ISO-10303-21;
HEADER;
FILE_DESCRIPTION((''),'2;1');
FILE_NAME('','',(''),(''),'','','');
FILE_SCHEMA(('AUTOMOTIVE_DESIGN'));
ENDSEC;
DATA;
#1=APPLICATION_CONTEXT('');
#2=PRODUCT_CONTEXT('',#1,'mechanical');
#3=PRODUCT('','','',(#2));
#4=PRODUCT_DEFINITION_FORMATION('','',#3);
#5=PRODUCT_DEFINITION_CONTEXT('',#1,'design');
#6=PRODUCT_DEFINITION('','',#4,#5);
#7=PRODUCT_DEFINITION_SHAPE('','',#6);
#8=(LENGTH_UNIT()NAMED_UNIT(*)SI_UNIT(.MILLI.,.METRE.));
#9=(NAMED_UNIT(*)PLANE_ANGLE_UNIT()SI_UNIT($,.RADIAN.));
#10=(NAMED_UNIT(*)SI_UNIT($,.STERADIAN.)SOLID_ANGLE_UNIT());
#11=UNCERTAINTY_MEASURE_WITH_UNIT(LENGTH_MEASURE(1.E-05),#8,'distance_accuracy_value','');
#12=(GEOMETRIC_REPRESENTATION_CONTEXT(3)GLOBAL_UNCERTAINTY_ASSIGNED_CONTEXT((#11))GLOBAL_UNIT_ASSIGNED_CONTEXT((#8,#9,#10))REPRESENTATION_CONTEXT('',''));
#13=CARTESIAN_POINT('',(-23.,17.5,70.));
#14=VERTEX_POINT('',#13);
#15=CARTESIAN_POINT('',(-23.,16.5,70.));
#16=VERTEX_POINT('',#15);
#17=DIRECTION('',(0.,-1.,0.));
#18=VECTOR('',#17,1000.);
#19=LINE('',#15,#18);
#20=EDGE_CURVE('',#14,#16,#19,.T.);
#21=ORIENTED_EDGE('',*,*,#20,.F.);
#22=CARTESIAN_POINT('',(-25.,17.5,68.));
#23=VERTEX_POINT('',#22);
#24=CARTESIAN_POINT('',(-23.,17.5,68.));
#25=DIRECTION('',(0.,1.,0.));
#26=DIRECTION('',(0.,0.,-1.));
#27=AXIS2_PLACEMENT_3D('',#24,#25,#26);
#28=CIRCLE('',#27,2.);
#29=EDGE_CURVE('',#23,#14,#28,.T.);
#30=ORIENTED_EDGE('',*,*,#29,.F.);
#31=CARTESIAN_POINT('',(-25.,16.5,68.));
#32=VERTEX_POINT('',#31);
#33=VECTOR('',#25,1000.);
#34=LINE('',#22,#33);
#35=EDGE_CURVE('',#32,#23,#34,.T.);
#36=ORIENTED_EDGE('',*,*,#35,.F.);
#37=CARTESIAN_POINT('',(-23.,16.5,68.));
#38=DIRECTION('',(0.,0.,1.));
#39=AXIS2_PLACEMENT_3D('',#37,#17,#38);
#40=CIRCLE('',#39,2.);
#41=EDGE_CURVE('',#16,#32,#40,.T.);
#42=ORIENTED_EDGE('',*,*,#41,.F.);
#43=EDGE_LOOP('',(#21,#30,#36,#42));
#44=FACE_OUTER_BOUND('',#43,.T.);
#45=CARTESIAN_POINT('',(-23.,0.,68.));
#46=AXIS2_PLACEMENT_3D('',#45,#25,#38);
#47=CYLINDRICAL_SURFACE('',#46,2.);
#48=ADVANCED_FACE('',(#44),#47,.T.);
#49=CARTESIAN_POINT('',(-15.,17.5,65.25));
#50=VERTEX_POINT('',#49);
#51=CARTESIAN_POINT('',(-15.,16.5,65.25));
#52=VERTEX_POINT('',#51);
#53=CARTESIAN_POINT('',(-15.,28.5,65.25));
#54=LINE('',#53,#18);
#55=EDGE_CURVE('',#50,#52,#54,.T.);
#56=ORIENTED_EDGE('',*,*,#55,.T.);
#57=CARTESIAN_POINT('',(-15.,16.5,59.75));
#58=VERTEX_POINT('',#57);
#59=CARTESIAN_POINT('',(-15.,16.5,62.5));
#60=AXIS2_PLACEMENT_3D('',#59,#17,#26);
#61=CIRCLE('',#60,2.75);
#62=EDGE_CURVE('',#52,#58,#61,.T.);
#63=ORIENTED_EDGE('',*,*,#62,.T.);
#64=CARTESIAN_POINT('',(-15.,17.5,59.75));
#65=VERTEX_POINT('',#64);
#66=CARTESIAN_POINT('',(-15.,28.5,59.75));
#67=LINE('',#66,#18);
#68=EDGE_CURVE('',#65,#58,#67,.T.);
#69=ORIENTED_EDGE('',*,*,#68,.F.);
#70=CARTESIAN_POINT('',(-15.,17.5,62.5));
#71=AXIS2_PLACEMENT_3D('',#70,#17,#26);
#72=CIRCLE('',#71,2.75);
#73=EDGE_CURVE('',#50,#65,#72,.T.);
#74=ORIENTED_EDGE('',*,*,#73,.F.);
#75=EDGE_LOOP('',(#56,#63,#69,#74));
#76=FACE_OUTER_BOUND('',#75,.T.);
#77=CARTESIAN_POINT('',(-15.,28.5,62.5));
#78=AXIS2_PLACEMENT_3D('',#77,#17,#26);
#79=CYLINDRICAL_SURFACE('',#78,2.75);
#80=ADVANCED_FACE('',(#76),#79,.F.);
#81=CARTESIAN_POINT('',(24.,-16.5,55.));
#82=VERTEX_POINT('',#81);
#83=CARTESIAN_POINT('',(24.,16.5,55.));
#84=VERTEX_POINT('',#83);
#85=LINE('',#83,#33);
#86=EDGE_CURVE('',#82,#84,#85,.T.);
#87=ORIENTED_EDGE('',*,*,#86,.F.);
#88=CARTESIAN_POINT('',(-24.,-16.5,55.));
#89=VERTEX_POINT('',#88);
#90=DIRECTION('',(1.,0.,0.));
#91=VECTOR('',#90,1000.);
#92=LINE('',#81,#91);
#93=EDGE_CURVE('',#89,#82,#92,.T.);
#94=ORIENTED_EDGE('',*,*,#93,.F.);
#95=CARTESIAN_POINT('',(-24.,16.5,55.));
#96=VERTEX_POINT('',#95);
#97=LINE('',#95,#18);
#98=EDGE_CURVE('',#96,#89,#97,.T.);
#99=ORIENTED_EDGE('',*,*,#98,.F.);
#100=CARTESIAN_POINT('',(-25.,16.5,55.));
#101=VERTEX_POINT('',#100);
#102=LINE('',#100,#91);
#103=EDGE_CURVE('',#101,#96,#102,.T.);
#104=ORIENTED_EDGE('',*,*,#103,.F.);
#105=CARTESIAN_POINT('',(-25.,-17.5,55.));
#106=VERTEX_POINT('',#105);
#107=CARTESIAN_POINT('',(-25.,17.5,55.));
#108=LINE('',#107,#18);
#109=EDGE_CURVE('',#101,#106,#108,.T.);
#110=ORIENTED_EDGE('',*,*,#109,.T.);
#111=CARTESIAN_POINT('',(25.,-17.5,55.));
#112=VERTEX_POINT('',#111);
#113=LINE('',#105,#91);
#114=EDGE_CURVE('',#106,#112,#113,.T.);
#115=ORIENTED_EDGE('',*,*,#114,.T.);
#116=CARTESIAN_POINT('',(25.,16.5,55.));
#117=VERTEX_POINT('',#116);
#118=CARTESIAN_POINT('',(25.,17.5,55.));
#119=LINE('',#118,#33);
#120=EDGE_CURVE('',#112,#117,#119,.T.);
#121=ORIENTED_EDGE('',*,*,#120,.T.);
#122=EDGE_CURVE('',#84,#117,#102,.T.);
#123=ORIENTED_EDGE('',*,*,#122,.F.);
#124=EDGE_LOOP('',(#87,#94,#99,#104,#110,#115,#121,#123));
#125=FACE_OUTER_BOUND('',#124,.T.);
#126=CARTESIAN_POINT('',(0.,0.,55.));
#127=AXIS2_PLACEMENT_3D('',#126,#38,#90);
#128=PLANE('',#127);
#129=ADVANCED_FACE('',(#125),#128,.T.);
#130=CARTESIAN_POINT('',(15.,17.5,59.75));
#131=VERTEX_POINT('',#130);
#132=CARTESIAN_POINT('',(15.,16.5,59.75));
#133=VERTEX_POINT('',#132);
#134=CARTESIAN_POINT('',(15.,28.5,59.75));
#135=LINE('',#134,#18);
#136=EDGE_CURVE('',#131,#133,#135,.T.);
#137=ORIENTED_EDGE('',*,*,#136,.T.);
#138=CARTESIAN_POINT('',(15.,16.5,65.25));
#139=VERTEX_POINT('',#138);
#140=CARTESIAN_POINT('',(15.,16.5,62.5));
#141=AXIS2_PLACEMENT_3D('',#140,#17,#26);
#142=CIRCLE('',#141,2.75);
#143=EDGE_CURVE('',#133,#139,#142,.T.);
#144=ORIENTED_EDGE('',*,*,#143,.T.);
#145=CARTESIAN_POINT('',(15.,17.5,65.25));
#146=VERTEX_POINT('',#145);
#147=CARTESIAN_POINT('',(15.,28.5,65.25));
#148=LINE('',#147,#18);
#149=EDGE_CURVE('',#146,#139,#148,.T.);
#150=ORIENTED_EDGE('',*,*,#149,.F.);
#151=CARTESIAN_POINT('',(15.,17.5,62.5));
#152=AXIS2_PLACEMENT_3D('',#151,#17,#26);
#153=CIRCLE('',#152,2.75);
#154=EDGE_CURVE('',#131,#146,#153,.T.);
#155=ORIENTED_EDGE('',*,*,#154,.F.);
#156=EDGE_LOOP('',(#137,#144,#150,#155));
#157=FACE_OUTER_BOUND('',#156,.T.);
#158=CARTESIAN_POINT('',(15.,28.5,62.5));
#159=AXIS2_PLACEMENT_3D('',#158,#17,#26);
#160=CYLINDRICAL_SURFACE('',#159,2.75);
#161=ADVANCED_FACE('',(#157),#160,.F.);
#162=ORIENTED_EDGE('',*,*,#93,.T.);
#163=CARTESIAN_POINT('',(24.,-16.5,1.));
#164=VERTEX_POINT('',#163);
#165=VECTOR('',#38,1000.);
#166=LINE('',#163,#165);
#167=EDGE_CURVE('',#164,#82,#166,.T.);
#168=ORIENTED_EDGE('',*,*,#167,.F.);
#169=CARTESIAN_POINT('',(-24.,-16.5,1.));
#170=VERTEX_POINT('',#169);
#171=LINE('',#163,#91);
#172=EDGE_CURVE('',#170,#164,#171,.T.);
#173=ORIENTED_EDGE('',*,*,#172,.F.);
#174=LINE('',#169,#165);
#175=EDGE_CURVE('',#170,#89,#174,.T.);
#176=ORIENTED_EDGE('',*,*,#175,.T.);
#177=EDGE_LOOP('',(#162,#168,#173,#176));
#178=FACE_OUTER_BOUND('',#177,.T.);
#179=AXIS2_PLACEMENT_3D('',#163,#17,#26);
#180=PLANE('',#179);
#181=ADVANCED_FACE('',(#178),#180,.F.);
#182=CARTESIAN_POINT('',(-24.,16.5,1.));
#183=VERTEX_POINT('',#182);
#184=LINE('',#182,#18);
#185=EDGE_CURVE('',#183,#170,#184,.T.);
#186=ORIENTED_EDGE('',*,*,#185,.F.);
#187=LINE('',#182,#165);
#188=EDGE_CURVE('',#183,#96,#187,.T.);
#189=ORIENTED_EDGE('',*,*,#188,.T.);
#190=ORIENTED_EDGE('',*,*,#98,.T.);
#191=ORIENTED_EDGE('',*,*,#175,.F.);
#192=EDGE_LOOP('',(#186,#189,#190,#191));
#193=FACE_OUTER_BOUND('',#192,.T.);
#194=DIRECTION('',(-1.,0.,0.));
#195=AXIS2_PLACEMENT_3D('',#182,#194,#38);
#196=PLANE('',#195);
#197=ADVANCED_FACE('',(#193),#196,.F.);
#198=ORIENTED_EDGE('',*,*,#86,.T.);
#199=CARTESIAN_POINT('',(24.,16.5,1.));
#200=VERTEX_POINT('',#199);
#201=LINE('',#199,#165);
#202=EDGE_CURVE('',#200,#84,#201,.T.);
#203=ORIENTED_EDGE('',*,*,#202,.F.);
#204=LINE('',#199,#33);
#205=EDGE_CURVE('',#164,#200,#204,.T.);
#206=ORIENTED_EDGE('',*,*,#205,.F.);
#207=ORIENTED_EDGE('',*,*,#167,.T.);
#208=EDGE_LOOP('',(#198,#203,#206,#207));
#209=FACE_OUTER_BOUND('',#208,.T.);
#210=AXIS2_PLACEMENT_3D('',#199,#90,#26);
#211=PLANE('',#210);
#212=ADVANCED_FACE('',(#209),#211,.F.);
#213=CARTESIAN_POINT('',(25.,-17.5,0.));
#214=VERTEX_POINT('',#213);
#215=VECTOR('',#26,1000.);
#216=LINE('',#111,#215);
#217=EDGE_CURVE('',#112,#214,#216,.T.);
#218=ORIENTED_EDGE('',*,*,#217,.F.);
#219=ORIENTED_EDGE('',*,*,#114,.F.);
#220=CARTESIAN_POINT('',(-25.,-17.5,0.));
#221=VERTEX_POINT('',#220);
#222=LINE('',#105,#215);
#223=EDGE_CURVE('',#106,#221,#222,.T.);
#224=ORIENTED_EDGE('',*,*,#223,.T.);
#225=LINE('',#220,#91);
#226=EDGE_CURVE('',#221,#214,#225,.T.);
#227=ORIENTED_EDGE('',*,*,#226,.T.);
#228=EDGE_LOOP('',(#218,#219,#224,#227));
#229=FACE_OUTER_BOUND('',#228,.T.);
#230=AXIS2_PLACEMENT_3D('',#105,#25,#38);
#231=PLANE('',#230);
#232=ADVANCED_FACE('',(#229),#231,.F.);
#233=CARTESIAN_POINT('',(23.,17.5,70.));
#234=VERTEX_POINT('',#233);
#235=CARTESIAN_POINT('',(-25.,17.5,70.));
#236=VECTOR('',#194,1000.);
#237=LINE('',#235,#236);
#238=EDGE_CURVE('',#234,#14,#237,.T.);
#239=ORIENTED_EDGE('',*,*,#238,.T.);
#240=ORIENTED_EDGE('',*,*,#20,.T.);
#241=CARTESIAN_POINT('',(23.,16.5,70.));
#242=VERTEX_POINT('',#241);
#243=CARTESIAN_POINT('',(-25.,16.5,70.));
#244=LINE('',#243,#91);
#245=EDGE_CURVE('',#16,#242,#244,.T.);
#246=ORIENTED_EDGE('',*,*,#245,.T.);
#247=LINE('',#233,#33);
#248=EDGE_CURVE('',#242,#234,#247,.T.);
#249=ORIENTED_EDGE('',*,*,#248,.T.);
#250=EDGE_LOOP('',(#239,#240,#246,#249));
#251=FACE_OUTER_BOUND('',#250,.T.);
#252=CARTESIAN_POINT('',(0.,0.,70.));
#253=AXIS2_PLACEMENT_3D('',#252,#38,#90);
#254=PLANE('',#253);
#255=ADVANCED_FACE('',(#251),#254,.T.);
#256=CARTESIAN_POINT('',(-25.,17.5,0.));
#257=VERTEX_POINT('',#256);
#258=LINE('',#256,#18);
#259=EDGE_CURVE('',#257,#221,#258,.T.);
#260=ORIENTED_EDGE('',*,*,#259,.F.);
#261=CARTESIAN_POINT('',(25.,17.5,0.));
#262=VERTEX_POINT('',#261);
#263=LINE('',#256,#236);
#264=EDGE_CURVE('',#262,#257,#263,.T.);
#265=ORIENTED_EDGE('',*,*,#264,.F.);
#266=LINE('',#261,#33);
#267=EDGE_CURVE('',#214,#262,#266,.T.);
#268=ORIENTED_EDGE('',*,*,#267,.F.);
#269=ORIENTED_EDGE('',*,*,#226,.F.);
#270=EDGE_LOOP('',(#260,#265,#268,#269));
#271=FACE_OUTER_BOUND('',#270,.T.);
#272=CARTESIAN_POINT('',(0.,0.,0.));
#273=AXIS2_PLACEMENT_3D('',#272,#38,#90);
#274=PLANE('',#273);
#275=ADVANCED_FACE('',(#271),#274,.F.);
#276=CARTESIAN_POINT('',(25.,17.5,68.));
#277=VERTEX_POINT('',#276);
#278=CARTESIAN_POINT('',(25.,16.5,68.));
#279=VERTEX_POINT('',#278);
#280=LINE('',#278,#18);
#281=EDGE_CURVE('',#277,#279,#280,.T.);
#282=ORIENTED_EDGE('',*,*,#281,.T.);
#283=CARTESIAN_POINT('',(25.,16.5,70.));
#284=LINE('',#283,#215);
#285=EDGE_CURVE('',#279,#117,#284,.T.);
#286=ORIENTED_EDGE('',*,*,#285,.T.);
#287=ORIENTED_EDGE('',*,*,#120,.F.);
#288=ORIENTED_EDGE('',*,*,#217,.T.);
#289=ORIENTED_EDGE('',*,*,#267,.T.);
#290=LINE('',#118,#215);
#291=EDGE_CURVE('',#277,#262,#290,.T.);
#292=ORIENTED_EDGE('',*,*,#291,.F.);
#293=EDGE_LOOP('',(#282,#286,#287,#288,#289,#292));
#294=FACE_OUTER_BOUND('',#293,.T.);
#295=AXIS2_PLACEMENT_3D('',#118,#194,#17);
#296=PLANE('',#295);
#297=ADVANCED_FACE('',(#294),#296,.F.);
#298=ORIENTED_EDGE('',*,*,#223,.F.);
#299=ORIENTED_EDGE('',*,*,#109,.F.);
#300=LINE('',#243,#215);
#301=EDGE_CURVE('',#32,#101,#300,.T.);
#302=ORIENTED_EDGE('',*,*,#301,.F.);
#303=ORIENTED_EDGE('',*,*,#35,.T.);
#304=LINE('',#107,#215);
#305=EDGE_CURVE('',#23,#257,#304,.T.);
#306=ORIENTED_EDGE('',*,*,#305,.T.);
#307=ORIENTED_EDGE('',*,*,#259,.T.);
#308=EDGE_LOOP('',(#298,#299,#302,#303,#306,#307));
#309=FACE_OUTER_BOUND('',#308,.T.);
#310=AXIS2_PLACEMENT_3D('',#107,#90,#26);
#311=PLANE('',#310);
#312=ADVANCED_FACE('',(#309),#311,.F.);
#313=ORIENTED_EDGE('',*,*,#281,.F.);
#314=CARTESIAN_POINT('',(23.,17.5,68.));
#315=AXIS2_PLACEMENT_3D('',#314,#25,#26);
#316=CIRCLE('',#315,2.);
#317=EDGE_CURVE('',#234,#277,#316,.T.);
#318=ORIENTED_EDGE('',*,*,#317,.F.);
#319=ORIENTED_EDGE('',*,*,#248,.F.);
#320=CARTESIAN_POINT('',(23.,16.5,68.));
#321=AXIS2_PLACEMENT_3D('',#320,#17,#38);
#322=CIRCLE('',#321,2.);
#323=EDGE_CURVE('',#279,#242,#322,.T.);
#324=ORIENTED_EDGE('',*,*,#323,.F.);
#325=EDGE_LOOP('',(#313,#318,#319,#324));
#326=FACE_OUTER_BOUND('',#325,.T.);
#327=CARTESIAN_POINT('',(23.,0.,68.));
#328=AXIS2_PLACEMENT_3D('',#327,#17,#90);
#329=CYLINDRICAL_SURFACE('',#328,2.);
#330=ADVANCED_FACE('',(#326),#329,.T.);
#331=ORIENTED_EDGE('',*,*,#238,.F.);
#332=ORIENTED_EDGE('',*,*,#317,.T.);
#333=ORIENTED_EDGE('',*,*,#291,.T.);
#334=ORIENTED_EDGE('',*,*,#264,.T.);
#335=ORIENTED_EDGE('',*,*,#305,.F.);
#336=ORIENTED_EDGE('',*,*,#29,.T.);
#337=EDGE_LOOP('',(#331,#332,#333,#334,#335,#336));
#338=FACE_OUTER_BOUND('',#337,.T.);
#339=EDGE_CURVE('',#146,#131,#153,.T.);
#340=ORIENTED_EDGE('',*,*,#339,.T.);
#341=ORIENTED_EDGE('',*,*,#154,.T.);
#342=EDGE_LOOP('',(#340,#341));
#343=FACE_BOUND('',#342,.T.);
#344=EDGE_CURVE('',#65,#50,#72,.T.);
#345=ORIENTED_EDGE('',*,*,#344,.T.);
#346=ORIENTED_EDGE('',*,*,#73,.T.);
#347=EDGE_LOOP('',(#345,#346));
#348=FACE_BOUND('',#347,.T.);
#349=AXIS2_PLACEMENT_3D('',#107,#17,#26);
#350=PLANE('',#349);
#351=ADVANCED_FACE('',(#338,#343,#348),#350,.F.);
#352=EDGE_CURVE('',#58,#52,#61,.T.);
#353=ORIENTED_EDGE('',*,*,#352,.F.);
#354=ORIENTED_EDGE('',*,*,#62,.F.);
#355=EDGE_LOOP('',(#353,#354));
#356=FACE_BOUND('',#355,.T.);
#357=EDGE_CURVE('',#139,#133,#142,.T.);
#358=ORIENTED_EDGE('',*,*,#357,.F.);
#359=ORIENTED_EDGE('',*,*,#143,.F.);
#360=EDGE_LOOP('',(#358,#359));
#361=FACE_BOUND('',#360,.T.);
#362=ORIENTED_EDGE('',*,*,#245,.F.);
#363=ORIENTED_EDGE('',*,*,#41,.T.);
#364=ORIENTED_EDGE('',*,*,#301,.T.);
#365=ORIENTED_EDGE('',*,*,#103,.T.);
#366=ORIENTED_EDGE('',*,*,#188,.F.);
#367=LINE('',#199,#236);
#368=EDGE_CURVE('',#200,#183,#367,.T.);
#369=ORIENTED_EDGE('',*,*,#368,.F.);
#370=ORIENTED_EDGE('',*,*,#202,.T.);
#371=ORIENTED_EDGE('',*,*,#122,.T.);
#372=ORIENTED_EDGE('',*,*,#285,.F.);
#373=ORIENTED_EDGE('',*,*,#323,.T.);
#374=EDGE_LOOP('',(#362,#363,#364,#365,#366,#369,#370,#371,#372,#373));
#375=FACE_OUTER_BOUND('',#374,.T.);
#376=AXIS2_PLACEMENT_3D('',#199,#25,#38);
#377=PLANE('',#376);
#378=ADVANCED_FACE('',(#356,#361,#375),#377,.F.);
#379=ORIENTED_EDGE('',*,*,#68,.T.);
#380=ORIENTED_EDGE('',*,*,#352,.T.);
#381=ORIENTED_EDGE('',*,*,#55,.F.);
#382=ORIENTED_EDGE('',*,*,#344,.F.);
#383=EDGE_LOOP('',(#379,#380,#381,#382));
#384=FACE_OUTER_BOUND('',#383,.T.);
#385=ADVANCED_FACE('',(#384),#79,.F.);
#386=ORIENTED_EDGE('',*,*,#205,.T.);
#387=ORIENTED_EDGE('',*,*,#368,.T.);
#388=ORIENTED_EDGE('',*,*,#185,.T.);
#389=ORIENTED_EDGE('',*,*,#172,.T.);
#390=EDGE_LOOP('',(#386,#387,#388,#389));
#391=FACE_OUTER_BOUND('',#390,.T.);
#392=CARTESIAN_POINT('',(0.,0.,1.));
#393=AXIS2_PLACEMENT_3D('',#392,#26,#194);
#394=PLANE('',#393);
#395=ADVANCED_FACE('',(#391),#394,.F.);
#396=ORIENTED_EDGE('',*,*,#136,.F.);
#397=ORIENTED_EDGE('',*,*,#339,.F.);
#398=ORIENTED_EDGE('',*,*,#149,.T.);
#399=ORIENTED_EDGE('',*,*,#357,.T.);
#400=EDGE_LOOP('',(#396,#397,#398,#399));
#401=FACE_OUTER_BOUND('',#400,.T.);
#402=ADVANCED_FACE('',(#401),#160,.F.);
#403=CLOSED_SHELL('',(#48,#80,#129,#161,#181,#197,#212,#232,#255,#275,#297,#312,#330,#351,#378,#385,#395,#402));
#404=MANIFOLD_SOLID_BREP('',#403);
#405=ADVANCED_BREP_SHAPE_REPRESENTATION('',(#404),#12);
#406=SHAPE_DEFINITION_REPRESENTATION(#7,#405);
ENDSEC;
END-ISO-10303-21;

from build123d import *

# Parameters (mm, degrees)
SKETCH_1_W          = 50
SKETCH_1_H          = 35
EXTRUDE_1_DEPTH     = 55
SKETCH_2_W          = 48
SKETCH_2_H          = 33
CUT_EXTRUDE_1_DEPTH = 54
SKETCH_5_W          = 50
SKETCH_5_H          = 1
EXTRUDE_2_DEPTH     = 15
SKETCH_6_R          = 2.75
CUT_EXTRUDE_3_DEPTH = 12
FILLET_1_R          = 2


with BuildPart() as part:
    # 草图1 → 凸台-拉伸1 (new body)
    with BuildSketch(Plane.XY):
        Rectangle(SKETCH_1_W, SKETCH_1_H)
    extrude(amount=EXTRUDE_1_DEPTH)

    # 草图2 → 切除-拉伸1 (cut)
    with BuildSketch(Plane.XY.offset(55)):
        Rectangle(SKETCH_2_W, SKETCH_2_H)
    extrude(amount=-CUT_EXTRUDE_1_DEPTH, mode=Mode.SUBTRACT)

    # 草图5 → 凸台-拉伸2 (add)
    with BuildSketch(Plane.XY.offset(55)):
        with Locations((0, 17)):
            Rectangle(SKETCH_5_W, SKETCH_5_H)
    extrude(amount=EXTRUDE_2_DEPTH)

    # 草图6 → 切除-拉伸3 (cut)
    with BuildSketch(Plane.XZ.offset(-16.5)):
        with Locations(Location((-15, 62.5, 0), (0, 0, 270))):
            Circle(SKETCH_6_R)
        with Locations(Location((15, 62.5, 0), (0, 0, 270))):
            Circle(SKETCH_6_R)
    extrude(amount=-CUT_EXTRUDE_3_DEPTH, mode=Mode.SUBTRACT)

    # 圆角1
    fillet_1_edges = [part.edges().sort_by_distance(p)[0] for p in [
        (25, 17, 70),
        (-25, 17, 70),
    ]]
    fillet(fillet_1_edges, radius=FILLET_1_R)


solid = part.part
